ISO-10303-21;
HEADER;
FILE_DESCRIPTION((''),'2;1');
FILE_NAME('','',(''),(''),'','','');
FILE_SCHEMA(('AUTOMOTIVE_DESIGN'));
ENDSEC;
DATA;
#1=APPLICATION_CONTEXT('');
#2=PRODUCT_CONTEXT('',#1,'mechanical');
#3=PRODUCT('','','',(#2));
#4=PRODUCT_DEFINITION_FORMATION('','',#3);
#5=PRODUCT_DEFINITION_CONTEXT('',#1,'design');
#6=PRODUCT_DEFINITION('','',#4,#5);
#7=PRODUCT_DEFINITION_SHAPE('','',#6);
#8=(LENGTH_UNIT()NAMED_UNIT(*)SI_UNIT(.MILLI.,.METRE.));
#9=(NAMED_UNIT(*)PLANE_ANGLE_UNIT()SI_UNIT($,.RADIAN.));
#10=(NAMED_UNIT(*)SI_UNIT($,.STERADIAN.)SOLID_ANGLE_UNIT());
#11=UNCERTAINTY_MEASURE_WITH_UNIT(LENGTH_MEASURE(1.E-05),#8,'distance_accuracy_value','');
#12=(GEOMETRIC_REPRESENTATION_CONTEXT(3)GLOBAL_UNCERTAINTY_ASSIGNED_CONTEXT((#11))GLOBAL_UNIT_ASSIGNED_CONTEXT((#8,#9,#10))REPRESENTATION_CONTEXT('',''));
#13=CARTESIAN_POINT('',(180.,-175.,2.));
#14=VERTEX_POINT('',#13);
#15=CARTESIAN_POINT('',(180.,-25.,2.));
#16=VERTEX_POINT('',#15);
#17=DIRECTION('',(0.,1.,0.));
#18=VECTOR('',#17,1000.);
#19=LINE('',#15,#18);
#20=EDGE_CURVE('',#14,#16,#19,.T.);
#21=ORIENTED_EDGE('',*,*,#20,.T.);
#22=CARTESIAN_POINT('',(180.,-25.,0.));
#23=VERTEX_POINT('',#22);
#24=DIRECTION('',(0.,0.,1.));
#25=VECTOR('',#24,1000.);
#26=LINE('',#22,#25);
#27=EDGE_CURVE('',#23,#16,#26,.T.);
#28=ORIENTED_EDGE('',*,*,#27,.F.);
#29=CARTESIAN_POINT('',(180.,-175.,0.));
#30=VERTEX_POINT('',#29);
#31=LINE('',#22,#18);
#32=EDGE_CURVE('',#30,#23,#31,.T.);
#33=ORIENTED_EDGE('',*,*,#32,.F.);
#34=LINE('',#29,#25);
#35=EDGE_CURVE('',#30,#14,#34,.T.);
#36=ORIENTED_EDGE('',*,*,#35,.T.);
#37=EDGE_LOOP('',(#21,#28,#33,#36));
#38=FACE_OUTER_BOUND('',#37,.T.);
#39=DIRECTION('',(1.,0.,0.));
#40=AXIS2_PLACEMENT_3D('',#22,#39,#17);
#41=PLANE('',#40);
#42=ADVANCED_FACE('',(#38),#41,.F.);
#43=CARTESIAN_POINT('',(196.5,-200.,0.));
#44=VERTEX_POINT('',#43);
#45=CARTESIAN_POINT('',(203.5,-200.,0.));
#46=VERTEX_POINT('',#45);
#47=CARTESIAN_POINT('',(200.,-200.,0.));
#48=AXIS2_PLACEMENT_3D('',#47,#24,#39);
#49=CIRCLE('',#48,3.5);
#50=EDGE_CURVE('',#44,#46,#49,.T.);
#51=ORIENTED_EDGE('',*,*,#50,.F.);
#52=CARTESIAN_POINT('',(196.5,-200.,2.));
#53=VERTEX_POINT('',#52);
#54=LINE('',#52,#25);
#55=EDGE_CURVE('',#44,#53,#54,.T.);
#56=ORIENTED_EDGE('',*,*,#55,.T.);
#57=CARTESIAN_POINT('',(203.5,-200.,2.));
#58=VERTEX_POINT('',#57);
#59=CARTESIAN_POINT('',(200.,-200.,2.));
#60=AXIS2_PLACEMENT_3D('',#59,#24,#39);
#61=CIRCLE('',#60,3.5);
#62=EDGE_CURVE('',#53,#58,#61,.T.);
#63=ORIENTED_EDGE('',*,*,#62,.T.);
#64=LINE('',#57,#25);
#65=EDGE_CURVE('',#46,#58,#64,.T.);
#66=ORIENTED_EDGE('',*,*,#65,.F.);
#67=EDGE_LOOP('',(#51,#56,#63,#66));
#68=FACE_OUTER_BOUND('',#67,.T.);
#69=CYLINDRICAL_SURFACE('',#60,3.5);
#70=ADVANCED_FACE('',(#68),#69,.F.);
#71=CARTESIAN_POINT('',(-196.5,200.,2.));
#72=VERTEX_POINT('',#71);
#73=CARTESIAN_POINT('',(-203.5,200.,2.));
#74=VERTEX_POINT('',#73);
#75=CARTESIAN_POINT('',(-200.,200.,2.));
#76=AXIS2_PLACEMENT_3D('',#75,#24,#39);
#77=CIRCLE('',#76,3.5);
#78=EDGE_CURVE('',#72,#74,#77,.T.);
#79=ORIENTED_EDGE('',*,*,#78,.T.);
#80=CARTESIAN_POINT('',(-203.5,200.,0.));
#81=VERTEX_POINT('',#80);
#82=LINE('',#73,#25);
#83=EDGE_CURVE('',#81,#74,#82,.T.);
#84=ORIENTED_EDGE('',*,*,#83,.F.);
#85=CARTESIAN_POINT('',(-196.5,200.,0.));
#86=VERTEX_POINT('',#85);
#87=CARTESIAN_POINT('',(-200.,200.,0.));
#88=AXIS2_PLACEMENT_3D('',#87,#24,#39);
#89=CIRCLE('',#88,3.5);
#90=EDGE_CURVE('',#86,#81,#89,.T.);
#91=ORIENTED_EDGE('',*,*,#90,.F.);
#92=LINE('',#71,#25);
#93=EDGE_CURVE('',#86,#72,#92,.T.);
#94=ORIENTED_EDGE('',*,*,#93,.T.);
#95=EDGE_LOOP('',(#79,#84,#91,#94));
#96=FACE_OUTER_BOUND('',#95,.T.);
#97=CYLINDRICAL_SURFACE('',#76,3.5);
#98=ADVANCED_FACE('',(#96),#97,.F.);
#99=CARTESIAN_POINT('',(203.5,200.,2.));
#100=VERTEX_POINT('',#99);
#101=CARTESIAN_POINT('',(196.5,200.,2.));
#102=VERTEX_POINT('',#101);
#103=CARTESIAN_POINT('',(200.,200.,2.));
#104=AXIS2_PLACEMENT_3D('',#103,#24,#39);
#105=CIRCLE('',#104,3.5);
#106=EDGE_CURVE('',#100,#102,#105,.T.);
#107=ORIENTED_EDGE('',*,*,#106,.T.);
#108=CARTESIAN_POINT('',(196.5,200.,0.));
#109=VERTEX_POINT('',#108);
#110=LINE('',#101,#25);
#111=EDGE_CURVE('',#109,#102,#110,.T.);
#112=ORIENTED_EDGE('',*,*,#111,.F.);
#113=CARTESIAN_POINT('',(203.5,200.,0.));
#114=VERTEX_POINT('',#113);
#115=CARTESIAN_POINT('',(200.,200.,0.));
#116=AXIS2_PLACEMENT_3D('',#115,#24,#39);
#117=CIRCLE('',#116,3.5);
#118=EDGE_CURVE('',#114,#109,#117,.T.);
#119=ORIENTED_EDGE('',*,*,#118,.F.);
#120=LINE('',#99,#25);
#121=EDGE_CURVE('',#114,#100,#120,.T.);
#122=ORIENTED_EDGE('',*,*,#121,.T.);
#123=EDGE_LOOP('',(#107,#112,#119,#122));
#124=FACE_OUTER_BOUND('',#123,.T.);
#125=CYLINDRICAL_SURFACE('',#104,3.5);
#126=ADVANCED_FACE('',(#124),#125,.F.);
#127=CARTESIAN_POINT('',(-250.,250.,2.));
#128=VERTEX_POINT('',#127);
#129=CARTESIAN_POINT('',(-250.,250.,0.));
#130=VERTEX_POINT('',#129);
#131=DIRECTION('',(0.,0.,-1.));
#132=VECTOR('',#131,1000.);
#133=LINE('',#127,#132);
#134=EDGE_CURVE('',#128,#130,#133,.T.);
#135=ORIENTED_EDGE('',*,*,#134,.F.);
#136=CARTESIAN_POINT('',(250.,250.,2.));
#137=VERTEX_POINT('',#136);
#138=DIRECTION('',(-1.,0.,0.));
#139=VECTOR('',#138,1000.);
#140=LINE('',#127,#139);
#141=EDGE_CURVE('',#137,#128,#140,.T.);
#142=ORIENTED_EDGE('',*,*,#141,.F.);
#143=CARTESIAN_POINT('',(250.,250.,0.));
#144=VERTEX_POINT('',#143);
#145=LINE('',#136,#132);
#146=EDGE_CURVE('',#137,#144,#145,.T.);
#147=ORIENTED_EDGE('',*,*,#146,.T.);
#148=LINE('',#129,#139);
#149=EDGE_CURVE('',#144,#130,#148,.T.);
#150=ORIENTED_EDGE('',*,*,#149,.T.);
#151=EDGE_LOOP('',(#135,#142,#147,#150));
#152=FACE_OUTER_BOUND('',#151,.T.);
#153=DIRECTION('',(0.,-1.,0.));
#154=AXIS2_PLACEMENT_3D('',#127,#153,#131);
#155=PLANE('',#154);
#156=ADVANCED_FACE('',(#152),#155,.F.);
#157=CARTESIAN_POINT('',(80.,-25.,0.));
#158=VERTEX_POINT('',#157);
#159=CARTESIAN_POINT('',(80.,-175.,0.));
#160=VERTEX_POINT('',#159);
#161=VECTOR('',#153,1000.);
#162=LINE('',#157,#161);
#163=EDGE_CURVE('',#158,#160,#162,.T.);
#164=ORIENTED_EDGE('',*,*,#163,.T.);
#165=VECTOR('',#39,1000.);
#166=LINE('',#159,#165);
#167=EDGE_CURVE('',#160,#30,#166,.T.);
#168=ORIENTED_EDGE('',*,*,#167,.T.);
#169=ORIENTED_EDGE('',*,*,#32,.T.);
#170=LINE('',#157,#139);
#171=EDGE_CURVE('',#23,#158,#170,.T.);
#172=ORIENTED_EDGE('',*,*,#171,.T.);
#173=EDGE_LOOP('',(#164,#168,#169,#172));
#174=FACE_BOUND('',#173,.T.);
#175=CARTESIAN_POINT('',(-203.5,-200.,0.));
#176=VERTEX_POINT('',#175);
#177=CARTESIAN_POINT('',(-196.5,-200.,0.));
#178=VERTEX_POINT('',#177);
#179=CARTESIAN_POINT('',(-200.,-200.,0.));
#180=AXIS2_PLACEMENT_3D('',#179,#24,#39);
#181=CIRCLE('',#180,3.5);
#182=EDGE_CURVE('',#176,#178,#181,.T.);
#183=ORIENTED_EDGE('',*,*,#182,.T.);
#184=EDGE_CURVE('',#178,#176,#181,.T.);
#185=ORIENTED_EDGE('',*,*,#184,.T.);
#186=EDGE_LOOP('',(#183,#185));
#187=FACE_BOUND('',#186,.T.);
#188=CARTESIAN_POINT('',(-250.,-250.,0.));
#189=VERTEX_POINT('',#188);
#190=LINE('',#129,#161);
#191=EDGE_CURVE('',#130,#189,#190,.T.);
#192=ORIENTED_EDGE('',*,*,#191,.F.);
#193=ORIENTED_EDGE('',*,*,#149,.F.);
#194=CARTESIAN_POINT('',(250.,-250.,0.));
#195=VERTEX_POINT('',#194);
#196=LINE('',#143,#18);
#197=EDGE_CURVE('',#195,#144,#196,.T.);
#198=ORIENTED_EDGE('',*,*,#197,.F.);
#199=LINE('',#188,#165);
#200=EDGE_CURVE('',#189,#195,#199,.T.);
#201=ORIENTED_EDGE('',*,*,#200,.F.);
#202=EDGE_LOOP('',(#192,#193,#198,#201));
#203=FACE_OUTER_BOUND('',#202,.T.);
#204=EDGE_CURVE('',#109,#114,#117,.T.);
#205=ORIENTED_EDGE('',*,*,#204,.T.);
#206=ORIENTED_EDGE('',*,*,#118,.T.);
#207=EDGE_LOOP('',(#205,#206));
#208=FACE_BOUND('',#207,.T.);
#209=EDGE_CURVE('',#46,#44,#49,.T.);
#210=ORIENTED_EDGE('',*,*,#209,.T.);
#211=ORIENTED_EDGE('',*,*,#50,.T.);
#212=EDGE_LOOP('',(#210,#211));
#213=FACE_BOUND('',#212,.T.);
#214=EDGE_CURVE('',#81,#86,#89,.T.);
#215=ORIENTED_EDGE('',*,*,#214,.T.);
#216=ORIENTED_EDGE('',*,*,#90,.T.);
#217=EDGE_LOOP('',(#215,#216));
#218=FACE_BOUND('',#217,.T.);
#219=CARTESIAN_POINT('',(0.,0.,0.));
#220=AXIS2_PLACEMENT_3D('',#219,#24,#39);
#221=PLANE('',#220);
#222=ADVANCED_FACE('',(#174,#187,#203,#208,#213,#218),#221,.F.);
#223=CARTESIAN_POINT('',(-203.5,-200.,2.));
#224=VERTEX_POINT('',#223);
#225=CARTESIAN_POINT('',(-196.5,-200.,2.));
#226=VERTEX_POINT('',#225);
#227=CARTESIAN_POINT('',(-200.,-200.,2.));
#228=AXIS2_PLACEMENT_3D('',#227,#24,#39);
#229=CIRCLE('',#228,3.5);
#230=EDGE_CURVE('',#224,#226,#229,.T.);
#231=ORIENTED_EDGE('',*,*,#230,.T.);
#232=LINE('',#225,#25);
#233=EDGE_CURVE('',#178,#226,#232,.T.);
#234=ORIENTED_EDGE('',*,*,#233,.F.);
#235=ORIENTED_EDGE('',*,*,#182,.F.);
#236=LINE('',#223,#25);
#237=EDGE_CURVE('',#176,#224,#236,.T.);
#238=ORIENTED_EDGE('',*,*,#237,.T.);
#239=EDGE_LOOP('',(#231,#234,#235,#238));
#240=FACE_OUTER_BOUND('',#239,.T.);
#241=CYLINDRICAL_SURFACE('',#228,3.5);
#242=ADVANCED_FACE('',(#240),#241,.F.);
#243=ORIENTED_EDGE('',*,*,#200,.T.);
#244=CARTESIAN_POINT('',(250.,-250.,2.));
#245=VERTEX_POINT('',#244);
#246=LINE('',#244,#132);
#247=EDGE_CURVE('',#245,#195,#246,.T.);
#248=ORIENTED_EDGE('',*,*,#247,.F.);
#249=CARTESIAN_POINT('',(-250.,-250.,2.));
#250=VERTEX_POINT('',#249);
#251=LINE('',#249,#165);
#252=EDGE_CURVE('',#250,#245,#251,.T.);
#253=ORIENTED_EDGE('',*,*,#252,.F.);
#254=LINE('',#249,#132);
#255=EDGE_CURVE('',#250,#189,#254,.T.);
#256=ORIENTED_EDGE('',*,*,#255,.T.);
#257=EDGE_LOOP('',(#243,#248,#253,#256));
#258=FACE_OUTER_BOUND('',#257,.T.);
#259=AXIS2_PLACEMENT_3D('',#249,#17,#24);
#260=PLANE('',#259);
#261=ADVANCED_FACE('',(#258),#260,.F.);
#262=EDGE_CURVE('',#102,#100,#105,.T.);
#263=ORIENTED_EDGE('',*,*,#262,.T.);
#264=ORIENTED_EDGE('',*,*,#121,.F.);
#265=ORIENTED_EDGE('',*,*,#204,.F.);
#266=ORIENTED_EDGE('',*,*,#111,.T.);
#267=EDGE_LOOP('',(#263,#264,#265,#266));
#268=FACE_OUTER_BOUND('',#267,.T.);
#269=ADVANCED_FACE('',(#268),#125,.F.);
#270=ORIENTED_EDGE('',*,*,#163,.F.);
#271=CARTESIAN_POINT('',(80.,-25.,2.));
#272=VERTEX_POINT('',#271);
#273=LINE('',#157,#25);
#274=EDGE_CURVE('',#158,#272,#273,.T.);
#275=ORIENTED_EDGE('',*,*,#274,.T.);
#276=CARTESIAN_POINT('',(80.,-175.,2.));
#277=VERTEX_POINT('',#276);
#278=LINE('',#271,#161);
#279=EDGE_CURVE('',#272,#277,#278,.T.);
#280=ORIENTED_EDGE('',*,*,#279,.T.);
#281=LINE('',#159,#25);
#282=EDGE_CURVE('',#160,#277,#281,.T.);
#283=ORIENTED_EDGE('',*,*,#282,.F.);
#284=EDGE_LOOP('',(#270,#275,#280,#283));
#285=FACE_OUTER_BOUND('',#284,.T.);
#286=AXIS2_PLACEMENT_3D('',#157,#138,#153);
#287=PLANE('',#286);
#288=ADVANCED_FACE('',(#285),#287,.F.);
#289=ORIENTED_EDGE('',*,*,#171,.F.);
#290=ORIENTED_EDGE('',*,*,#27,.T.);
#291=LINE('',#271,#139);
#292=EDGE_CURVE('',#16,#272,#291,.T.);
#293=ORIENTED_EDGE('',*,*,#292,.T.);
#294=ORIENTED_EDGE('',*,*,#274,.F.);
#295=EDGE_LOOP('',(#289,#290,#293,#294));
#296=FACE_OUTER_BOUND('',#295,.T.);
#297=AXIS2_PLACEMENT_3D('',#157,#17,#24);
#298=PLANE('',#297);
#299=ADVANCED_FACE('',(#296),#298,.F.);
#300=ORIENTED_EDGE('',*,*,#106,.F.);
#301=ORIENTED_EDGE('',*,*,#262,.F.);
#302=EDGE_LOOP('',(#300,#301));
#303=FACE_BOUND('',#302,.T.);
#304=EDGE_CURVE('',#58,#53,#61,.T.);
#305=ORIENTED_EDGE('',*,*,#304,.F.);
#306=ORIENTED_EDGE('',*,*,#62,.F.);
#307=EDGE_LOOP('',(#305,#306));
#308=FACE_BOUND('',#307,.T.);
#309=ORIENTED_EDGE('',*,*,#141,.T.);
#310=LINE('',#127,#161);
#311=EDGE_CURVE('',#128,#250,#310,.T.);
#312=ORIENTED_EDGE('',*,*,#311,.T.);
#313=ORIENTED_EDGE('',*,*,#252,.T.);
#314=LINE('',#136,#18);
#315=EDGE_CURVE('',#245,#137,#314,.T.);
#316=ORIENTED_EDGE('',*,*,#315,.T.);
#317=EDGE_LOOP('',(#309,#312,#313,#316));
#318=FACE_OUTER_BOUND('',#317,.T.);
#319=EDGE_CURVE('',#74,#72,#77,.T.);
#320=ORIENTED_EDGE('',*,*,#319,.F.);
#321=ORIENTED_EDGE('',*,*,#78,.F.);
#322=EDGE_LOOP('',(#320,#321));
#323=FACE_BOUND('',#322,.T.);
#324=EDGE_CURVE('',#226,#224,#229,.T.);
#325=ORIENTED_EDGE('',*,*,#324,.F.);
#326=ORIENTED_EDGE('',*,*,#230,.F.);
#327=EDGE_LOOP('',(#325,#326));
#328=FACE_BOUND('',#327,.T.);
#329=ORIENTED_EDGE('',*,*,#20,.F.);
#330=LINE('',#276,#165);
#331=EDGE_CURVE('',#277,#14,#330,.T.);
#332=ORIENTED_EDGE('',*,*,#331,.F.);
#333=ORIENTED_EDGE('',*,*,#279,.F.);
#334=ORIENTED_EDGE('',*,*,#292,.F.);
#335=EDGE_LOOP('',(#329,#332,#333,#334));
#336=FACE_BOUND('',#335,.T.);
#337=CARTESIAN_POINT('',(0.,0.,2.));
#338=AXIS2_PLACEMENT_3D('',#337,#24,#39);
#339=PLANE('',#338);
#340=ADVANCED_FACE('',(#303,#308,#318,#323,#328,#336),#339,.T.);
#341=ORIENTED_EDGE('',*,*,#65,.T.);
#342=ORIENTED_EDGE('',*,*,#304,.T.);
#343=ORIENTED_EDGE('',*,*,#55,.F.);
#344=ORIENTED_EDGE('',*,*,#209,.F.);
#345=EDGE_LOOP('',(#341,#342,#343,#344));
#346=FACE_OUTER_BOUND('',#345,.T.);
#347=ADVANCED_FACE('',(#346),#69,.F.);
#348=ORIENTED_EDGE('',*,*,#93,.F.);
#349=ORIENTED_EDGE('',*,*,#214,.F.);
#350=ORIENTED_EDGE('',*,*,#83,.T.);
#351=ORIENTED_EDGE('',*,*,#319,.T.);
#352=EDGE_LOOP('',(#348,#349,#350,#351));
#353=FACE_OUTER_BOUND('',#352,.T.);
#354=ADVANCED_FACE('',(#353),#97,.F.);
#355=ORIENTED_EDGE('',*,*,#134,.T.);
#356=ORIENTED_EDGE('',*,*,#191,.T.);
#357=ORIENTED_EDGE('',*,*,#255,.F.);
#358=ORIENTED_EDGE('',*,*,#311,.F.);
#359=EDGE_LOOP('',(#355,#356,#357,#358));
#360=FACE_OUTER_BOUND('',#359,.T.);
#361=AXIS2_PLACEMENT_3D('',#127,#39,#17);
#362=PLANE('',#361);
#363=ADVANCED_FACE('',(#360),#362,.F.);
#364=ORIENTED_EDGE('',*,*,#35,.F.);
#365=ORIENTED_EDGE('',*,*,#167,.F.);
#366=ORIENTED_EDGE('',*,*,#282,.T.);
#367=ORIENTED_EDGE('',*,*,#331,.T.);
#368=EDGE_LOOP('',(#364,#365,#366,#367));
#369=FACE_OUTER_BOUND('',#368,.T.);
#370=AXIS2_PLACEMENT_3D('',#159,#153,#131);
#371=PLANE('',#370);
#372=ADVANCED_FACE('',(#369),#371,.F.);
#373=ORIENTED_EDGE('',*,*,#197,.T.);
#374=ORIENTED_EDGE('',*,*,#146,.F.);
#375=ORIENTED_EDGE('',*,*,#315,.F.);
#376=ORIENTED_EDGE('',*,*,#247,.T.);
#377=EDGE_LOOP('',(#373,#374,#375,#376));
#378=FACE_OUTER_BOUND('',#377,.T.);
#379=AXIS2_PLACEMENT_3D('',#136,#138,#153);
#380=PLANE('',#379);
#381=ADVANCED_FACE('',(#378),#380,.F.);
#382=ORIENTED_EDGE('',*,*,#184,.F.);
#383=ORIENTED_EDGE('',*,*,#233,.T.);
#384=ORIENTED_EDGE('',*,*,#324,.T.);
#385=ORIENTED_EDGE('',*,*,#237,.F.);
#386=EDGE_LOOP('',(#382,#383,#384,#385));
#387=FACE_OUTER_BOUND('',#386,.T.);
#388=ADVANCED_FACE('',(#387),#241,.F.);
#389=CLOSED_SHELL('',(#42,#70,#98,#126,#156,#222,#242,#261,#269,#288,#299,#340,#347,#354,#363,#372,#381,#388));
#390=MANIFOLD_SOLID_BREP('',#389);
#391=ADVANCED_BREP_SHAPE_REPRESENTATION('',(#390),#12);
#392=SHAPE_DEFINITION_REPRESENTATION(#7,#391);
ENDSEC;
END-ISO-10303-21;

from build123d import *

# Parameters (mm, degrees)
SKETCH_1_W            = 500
SKETCH_1_H            = 500
EXTRUDE_1_DEPTH       = 2
HOLE_WIZARD_7_0_7_1_D = 7
SKETCH_4_W            = 100
SKETCH_4_H            = 150
CUT_EXTRUDE_1_DEPTH   = 354.559047402


with BuildPart() as part:
    # 草图1 → 凸台-拉伸1 (new body)
    with BuildSketch(Plane.XY):
        Rectangle(SKETCH_1_W, SKETCH_1_H)
    extrude(amount=EXTRUDE_1_DEPTH)

    # Ø7.0 (7) 直径孔1 (through all)
    with Locations(Plane.XY.offset(2)):
        with Locations((-200, 200), (200, 200), (-200, -200), (200, -200)):
            Hole(HOLE_WIZARD_7_0_7_1_D / 2)

    # 草图4 → 切除-拉伸1 (cut, through all)
    with BuildSketch(Plane.XY.offset(2)):
        with Locations((130, -100)):
            Rectangle(SKETCH_4_W, SKETCH_4_H)
    extrude(amount=-CUT_EXTRUDE_1_DEPTH, mode=Mode.SUBTRACT)


solid = part.part
